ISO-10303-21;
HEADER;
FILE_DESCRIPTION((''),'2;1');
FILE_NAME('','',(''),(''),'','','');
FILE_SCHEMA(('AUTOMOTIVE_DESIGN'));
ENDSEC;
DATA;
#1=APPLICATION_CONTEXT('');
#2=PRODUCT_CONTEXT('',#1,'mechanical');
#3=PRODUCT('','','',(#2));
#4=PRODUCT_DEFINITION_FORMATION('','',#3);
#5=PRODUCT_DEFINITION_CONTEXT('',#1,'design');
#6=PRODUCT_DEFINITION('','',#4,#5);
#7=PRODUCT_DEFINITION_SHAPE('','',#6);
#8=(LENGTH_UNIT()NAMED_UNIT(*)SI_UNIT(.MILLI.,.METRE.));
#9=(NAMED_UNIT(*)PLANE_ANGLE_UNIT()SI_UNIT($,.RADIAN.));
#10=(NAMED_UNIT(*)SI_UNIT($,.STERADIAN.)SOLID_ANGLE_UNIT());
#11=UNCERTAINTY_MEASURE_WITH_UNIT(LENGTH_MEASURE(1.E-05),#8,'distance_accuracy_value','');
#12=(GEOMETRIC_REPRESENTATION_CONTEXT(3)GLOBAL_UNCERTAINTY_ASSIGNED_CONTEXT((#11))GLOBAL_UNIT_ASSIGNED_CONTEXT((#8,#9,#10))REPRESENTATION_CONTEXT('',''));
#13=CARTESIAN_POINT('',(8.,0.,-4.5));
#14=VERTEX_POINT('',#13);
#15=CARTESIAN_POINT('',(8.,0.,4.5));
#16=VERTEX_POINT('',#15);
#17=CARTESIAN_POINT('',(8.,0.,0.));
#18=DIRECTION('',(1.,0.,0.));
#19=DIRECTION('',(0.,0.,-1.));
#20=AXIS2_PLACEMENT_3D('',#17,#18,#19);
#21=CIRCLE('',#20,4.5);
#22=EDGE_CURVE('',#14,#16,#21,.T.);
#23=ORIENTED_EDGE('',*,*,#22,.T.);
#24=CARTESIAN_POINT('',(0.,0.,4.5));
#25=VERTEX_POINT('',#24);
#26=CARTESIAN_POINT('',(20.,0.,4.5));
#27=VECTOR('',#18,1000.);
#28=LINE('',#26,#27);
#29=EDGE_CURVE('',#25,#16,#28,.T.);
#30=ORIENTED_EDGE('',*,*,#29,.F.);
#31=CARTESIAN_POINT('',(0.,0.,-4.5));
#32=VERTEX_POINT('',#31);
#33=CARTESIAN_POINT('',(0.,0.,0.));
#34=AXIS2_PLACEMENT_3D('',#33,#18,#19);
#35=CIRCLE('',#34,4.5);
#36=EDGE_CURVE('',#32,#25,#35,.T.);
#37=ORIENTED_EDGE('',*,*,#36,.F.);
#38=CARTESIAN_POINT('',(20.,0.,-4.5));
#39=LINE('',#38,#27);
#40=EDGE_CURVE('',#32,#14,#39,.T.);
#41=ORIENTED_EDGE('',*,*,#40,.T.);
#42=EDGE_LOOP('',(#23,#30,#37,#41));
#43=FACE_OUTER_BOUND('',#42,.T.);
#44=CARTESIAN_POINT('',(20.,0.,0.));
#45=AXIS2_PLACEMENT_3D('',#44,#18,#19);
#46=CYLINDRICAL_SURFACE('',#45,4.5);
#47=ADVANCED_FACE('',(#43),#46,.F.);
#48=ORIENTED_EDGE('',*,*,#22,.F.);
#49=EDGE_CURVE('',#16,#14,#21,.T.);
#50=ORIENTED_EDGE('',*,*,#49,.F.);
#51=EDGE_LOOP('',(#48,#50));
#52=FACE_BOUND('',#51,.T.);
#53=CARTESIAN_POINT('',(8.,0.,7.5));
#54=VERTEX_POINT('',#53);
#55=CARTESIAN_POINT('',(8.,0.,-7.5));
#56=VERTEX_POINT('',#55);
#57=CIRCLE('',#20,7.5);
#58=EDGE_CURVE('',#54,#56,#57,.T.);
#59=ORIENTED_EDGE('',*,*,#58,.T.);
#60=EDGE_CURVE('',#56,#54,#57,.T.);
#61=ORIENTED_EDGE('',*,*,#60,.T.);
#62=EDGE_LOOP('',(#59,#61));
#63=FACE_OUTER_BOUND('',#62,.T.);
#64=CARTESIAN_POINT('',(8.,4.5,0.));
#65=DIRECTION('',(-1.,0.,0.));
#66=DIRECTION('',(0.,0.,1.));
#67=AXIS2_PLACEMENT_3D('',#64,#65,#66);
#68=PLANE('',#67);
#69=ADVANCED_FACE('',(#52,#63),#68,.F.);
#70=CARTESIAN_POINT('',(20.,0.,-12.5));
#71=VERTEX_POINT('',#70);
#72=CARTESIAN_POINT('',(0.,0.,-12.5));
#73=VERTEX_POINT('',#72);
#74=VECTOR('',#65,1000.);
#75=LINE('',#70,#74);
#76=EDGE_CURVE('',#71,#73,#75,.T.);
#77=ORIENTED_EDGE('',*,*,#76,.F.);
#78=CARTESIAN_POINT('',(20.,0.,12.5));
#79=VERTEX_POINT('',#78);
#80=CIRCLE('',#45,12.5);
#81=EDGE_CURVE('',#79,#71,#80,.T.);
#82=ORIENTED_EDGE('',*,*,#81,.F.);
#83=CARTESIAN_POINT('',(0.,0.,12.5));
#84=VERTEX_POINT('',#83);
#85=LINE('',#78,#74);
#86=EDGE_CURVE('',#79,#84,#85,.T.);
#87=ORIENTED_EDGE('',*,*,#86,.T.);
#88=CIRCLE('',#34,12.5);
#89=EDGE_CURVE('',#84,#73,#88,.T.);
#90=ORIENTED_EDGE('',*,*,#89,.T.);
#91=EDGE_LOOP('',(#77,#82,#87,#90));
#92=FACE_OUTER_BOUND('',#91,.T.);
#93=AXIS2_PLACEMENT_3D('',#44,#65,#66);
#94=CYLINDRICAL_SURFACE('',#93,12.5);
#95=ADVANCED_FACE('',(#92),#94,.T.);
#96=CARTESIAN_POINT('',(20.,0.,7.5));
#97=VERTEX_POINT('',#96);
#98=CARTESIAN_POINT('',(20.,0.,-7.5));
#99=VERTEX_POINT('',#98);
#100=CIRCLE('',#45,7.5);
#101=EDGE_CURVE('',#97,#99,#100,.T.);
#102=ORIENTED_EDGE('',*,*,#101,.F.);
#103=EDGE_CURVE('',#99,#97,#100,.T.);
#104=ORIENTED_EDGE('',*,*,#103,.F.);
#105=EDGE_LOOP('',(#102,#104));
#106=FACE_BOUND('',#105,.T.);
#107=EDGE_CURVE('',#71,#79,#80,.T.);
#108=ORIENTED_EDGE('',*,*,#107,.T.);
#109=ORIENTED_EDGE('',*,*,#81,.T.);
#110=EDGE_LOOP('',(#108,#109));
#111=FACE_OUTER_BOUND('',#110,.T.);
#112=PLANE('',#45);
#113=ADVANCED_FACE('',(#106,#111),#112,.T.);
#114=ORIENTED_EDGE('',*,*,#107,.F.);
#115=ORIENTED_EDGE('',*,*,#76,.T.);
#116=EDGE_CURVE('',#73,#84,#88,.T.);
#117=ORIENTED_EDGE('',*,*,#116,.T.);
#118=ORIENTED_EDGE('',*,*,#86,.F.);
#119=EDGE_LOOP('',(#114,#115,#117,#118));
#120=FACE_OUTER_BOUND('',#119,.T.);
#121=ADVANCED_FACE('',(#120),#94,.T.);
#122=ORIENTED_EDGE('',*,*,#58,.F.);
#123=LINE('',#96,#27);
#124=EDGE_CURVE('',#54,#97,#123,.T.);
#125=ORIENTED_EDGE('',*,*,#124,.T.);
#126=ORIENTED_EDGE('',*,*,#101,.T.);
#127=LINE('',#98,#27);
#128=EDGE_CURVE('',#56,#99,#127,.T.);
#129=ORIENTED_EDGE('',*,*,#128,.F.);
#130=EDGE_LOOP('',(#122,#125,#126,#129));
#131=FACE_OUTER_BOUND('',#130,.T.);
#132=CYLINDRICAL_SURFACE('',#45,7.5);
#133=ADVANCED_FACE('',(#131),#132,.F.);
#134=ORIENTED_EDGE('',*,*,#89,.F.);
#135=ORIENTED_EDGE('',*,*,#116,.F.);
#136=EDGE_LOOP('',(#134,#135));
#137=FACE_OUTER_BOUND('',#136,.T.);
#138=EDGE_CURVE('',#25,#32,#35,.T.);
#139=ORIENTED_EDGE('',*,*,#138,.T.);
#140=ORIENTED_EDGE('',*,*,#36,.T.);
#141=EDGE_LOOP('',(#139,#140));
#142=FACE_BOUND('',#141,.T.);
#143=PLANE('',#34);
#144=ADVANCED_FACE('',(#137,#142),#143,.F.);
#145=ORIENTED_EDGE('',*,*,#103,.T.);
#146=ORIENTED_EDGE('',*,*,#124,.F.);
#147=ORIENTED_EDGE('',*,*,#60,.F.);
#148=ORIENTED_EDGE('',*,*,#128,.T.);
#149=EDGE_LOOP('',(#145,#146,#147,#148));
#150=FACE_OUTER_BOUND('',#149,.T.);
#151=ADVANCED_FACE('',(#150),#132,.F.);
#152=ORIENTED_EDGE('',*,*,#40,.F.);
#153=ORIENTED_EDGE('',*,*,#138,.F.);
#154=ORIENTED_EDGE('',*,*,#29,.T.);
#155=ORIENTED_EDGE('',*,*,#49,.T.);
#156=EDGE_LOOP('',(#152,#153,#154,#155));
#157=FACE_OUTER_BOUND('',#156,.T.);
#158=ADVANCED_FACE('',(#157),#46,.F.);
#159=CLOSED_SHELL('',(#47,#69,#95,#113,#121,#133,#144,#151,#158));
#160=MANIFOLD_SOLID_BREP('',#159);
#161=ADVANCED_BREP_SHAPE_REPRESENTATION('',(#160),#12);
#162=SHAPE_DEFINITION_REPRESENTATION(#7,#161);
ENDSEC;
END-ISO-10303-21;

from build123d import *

# Parameters (mm, degrees)
SKETCH_1_R                = 12.5
EXTRUDE_1_DEPTH           = 20
HOLE_WIZARD_1_D           = 9
HOLE_WIZARD_1_CBORE_D     = 15
HOLE_WIZARD_1_CBORE_DEPTH = 12


with BuildPart() as part:
    # 草图1 → 凸台-拉伸1 (new body)
    with BuildSketch(Plane(origin=(0, 0, 0), x_dir=(0, 0, -1), z_dir=(1, 0, 0))):
        Circle(SKETCH_1_R)
    extrude(amount=EXTRUDE_1_DEPTH)

    # 打孔尺寸(%根据)内六角圆柱头螺钉的类型1 (through all)
    with Locations(Plane(origin=(20, 0, 0), x_dir=(0, 0, -1), z_dir=(1, 0, 0))):
        with Locations((0, 0)):
            CounterBoreHole(HOLE_WIZARD_1_D / 2, HOLE_WIZARD_1_CBORE_D / 2, HOLE_WIZARD_1_CBORE_DEPTH)


solid = part.part
